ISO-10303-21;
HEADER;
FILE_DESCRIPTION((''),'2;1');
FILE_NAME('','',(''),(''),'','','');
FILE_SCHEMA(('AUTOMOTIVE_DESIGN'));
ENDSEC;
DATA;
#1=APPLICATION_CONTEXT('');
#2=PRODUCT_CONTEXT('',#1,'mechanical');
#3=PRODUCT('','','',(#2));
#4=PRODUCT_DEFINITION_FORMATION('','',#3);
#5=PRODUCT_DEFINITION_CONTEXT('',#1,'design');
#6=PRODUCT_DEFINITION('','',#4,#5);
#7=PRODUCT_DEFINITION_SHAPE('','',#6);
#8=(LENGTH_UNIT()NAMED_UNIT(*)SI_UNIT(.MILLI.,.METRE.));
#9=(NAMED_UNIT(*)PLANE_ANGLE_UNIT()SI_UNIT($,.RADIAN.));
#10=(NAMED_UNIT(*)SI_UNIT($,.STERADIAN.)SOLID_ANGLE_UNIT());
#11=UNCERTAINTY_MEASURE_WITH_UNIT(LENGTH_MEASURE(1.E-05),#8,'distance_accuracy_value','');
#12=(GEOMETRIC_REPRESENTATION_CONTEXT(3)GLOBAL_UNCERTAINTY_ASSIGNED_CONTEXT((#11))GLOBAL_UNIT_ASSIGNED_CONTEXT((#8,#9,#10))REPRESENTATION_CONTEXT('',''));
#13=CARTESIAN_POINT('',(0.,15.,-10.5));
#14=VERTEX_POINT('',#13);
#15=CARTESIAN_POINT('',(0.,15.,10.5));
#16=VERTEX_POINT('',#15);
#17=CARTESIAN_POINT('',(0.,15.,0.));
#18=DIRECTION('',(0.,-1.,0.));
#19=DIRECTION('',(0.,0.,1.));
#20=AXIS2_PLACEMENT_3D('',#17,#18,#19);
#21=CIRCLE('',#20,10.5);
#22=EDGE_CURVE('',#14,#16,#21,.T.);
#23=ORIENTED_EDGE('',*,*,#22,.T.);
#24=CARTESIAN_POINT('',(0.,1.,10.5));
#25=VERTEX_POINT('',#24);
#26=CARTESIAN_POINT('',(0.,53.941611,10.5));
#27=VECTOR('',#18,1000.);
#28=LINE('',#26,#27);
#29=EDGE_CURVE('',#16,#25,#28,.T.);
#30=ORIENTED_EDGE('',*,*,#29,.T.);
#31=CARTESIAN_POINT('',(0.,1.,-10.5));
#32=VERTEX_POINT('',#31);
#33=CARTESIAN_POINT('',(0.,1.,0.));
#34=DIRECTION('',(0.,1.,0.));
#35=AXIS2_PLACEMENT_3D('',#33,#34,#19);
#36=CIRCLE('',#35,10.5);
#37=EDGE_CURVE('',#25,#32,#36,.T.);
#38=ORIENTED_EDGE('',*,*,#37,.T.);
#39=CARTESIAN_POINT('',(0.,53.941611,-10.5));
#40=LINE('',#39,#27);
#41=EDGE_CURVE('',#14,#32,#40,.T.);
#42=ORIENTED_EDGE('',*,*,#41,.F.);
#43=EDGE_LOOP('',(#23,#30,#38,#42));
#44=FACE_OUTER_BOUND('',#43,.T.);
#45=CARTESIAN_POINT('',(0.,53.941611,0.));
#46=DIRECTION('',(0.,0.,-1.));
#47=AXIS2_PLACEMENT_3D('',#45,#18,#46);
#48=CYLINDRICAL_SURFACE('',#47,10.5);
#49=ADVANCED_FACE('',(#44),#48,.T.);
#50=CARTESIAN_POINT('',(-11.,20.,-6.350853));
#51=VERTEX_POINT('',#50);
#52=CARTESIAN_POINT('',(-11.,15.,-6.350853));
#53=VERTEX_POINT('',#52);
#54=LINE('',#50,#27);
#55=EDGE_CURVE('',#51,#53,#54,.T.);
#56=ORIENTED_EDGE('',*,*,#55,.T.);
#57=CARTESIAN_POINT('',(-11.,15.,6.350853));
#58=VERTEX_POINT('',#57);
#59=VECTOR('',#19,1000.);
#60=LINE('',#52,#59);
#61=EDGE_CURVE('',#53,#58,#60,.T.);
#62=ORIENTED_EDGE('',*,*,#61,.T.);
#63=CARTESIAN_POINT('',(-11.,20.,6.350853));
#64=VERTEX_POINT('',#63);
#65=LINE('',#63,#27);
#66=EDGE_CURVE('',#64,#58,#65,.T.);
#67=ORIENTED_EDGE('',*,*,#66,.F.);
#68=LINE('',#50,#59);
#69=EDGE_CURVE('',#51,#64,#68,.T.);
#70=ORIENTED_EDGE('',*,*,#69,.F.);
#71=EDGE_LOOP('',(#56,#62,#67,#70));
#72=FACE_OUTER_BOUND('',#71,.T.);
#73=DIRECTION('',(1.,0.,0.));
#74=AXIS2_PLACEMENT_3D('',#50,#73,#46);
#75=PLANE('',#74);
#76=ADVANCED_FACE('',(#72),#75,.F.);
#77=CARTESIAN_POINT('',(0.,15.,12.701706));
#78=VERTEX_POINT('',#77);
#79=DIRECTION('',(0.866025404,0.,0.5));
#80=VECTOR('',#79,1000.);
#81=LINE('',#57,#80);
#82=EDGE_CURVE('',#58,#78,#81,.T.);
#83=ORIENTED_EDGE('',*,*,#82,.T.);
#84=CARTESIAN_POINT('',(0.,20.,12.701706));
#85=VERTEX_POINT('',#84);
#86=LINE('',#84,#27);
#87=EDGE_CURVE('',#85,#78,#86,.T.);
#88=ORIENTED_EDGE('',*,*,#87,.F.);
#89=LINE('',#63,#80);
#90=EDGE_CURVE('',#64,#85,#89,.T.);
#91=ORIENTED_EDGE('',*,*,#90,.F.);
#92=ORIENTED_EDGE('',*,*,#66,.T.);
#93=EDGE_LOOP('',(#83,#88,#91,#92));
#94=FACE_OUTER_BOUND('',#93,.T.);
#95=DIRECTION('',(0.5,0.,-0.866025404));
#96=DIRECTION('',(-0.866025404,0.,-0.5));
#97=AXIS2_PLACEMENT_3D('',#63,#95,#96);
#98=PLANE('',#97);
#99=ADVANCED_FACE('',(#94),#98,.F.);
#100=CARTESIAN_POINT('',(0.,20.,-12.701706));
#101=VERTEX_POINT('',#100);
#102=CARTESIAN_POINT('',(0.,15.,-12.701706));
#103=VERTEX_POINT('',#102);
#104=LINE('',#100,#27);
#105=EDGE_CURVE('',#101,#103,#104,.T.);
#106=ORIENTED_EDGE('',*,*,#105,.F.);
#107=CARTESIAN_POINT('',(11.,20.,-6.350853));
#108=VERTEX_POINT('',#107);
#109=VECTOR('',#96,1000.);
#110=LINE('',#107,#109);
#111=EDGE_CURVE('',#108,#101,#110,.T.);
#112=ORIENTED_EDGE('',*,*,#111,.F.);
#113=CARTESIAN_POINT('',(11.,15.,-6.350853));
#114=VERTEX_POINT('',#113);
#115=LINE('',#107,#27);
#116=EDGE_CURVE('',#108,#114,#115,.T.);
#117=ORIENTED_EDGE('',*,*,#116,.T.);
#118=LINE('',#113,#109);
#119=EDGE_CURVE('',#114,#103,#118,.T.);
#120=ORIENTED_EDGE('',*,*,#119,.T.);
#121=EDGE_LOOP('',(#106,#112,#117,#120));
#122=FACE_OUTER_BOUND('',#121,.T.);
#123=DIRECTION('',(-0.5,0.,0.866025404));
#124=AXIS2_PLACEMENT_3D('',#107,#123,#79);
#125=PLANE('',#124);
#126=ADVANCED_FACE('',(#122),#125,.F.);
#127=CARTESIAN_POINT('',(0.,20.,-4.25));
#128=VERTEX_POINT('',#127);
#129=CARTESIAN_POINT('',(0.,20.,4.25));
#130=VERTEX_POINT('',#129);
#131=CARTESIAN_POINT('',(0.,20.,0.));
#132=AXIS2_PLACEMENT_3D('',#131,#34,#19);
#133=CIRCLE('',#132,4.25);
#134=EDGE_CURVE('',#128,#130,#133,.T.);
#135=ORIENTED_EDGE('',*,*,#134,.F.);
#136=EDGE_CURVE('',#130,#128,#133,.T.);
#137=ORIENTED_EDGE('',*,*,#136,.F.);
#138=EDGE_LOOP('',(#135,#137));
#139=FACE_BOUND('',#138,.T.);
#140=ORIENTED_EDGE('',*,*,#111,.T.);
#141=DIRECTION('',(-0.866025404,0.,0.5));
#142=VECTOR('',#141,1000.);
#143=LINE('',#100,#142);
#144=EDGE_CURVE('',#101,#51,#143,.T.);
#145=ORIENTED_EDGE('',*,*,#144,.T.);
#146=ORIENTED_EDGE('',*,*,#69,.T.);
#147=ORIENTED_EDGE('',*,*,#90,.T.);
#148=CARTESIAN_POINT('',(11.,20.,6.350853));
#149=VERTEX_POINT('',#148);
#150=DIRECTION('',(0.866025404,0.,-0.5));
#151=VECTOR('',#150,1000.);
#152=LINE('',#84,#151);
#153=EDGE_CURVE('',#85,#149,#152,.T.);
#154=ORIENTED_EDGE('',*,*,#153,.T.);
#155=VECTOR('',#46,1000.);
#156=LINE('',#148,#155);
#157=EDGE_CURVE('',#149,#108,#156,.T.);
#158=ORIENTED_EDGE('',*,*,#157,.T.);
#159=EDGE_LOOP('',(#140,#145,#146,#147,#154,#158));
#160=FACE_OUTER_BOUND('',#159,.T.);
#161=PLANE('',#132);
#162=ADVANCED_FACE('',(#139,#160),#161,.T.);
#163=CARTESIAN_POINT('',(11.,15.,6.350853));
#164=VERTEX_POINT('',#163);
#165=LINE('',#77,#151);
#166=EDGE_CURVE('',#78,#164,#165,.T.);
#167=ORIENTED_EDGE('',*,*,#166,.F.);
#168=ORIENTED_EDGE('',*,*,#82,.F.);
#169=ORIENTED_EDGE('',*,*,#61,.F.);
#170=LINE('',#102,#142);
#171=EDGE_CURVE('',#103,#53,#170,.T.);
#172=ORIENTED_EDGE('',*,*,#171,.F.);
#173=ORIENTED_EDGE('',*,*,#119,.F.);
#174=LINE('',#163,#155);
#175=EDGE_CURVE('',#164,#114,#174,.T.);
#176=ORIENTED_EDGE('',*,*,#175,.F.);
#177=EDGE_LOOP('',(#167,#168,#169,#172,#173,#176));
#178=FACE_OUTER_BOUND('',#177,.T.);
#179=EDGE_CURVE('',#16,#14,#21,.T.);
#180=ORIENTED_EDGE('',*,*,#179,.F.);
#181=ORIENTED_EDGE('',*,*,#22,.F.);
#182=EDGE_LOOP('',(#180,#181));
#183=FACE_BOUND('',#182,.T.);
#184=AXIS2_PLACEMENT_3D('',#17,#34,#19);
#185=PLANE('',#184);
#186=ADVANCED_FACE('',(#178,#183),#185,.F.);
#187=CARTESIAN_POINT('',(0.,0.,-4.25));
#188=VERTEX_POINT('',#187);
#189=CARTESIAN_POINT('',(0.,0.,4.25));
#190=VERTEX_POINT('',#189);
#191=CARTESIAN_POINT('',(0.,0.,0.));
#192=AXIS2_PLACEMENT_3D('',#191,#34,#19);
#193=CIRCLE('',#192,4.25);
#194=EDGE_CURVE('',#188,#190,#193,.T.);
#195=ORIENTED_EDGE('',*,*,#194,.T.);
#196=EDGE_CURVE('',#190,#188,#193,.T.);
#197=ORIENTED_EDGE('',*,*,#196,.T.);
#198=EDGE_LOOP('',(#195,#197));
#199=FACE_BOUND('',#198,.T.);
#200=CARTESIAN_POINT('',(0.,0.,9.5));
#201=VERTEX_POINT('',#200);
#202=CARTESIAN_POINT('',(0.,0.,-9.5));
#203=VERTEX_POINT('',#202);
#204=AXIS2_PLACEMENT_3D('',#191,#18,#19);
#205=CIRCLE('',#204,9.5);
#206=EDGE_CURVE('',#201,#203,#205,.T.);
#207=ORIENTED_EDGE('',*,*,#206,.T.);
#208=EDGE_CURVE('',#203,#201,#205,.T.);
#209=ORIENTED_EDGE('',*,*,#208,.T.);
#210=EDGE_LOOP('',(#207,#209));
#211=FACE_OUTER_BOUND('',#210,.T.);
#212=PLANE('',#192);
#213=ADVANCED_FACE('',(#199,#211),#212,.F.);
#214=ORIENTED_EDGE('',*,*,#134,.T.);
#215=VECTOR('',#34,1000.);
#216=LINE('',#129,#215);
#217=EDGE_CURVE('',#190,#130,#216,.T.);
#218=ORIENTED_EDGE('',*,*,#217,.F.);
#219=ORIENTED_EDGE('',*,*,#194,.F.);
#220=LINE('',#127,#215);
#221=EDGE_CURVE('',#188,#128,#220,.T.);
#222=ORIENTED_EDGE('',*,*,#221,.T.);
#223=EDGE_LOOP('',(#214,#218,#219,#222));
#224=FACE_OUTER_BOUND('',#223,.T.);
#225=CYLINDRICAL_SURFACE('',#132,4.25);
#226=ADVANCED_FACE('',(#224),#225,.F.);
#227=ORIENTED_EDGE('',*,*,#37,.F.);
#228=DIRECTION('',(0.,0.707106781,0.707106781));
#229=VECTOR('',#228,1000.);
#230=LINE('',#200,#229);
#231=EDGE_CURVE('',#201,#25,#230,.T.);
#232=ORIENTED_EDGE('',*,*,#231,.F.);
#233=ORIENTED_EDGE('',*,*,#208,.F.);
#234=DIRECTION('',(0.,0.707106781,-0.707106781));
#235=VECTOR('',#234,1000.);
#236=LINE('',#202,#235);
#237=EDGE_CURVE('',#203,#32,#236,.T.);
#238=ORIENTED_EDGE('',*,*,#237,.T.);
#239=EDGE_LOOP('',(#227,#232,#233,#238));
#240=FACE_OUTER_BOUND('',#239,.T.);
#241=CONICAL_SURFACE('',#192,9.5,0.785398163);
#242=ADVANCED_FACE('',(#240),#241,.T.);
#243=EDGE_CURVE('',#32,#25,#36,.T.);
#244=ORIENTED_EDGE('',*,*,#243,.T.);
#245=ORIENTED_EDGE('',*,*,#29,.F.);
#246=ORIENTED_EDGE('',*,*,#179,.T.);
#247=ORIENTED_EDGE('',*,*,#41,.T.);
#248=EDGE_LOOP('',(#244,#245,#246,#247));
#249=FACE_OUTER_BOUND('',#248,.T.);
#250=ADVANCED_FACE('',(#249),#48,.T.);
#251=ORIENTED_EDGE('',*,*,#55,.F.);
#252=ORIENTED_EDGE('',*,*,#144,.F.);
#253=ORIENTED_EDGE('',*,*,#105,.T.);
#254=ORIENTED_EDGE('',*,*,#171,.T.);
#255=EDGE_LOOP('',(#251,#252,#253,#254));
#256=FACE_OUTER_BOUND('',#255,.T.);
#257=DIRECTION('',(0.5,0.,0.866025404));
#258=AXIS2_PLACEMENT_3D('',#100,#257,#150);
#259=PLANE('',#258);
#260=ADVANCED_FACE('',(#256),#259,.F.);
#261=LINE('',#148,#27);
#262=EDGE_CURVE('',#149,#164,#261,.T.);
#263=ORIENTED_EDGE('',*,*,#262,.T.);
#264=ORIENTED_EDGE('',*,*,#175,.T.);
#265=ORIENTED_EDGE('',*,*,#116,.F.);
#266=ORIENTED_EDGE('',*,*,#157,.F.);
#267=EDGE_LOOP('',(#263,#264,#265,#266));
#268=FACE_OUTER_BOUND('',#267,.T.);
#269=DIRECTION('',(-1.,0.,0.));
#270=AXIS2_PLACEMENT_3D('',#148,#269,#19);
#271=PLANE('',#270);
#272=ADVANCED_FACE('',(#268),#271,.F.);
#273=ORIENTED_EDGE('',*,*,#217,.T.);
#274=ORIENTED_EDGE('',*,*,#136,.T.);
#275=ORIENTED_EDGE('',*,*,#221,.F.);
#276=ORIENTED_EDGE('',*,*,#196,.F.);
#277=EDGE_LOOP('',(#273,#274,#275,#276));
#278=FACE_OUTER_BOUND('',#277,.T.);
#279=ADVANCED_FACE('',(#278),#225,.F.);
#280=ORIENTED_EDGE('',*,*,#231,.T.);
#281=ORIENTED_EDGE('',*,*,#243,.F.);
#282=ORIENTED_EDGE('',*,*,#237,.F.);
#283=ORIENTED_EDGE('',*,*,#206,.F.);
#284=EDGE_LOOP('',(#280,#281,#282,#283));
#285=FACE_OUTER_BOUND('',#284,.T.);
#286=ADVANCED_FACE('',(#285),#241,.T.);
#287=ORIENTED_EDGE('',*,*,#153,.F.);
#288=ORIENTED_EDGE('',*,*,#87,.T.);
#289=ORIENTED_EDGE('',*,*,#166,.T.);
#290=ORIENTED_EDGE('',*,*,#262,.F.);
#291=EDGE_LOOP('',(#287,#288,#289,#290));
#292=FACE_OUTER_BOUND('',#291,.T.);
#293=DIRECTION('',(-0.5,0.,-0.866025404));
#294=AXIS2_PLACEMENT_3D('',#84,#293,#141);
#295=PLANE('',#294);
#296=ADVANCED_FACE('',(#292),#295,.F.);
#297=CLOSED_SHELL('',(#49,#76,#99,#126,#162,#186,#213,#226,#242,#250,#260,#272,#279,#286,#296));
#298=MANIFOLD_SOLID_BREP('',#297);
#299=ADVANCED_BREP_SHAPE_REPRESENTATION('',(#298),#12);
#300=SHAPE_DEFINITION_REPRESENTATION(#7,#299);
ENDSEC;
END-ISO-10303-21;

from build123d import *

# Parameters (mm, degrees)
BOSS_EXTRUDE1_DEPTH = 20
SKETCH3_OUTSIDE_W   = 31.822
SKETCH3_OUTSIDE_H   = 35.226
SKETCH3_OUTSIDE_R   = 10.5
CUT_EXTRUDE1_DEPTH  = 15
CHAMFER1_SIZE       = 1
M10_TAPPED_HOLE1_D  = 8.5


with BuildPart() as part:
    # Sketch1 → Boss-Extrude1 (new body)
    with BuildSketch(Plane(origin=(0, 0, 0), x_dir=(1, 0, 0), z_dir=(0, 1, 0))):
        Polygon((11, -6.350852961), (11, 6.350852961), (0, 12.701705922), (-11, 6.350852961), (-11, -6.350852961), (0, -12.701705922), align=None)
    extrude(amount=BOSS_EXTRUDE1_DEPTH)

    # Sketch3 outside → Cut-Extrude1 (cut)
    with BuildSketch(Plane.XZ):
        Rectangle(SKETCH3_OUTSIDE_W, SKETCH3_OUTSIDE_H)
        with Locations(Location((0, 0, 0), (0, 0, 270))):
            Circle(SKETCH3_OUTSIDE_R, mode=Mode.SUBTRACT)
    extrude(amount=-CUT_EXTRUDE1_DEPTH, mode=Mode.SUBTRACT)

    # Chamfer1
    chamfer1_edges = [part.edges().sort_by_distance(p)[0] for p in [
        (0, 0, 10.5),
    ]]
    chamfer(chamfer1_edges, length=CHAMFER1_SIZE)

    # M10 Tapped Hole1 (through all)
    with Locations(Plane.ZX.offset(20)):
        with Locations((0, 0)):
            Hole(M10_TAPPED_HOLE1_D / 2)


solid = part.part
